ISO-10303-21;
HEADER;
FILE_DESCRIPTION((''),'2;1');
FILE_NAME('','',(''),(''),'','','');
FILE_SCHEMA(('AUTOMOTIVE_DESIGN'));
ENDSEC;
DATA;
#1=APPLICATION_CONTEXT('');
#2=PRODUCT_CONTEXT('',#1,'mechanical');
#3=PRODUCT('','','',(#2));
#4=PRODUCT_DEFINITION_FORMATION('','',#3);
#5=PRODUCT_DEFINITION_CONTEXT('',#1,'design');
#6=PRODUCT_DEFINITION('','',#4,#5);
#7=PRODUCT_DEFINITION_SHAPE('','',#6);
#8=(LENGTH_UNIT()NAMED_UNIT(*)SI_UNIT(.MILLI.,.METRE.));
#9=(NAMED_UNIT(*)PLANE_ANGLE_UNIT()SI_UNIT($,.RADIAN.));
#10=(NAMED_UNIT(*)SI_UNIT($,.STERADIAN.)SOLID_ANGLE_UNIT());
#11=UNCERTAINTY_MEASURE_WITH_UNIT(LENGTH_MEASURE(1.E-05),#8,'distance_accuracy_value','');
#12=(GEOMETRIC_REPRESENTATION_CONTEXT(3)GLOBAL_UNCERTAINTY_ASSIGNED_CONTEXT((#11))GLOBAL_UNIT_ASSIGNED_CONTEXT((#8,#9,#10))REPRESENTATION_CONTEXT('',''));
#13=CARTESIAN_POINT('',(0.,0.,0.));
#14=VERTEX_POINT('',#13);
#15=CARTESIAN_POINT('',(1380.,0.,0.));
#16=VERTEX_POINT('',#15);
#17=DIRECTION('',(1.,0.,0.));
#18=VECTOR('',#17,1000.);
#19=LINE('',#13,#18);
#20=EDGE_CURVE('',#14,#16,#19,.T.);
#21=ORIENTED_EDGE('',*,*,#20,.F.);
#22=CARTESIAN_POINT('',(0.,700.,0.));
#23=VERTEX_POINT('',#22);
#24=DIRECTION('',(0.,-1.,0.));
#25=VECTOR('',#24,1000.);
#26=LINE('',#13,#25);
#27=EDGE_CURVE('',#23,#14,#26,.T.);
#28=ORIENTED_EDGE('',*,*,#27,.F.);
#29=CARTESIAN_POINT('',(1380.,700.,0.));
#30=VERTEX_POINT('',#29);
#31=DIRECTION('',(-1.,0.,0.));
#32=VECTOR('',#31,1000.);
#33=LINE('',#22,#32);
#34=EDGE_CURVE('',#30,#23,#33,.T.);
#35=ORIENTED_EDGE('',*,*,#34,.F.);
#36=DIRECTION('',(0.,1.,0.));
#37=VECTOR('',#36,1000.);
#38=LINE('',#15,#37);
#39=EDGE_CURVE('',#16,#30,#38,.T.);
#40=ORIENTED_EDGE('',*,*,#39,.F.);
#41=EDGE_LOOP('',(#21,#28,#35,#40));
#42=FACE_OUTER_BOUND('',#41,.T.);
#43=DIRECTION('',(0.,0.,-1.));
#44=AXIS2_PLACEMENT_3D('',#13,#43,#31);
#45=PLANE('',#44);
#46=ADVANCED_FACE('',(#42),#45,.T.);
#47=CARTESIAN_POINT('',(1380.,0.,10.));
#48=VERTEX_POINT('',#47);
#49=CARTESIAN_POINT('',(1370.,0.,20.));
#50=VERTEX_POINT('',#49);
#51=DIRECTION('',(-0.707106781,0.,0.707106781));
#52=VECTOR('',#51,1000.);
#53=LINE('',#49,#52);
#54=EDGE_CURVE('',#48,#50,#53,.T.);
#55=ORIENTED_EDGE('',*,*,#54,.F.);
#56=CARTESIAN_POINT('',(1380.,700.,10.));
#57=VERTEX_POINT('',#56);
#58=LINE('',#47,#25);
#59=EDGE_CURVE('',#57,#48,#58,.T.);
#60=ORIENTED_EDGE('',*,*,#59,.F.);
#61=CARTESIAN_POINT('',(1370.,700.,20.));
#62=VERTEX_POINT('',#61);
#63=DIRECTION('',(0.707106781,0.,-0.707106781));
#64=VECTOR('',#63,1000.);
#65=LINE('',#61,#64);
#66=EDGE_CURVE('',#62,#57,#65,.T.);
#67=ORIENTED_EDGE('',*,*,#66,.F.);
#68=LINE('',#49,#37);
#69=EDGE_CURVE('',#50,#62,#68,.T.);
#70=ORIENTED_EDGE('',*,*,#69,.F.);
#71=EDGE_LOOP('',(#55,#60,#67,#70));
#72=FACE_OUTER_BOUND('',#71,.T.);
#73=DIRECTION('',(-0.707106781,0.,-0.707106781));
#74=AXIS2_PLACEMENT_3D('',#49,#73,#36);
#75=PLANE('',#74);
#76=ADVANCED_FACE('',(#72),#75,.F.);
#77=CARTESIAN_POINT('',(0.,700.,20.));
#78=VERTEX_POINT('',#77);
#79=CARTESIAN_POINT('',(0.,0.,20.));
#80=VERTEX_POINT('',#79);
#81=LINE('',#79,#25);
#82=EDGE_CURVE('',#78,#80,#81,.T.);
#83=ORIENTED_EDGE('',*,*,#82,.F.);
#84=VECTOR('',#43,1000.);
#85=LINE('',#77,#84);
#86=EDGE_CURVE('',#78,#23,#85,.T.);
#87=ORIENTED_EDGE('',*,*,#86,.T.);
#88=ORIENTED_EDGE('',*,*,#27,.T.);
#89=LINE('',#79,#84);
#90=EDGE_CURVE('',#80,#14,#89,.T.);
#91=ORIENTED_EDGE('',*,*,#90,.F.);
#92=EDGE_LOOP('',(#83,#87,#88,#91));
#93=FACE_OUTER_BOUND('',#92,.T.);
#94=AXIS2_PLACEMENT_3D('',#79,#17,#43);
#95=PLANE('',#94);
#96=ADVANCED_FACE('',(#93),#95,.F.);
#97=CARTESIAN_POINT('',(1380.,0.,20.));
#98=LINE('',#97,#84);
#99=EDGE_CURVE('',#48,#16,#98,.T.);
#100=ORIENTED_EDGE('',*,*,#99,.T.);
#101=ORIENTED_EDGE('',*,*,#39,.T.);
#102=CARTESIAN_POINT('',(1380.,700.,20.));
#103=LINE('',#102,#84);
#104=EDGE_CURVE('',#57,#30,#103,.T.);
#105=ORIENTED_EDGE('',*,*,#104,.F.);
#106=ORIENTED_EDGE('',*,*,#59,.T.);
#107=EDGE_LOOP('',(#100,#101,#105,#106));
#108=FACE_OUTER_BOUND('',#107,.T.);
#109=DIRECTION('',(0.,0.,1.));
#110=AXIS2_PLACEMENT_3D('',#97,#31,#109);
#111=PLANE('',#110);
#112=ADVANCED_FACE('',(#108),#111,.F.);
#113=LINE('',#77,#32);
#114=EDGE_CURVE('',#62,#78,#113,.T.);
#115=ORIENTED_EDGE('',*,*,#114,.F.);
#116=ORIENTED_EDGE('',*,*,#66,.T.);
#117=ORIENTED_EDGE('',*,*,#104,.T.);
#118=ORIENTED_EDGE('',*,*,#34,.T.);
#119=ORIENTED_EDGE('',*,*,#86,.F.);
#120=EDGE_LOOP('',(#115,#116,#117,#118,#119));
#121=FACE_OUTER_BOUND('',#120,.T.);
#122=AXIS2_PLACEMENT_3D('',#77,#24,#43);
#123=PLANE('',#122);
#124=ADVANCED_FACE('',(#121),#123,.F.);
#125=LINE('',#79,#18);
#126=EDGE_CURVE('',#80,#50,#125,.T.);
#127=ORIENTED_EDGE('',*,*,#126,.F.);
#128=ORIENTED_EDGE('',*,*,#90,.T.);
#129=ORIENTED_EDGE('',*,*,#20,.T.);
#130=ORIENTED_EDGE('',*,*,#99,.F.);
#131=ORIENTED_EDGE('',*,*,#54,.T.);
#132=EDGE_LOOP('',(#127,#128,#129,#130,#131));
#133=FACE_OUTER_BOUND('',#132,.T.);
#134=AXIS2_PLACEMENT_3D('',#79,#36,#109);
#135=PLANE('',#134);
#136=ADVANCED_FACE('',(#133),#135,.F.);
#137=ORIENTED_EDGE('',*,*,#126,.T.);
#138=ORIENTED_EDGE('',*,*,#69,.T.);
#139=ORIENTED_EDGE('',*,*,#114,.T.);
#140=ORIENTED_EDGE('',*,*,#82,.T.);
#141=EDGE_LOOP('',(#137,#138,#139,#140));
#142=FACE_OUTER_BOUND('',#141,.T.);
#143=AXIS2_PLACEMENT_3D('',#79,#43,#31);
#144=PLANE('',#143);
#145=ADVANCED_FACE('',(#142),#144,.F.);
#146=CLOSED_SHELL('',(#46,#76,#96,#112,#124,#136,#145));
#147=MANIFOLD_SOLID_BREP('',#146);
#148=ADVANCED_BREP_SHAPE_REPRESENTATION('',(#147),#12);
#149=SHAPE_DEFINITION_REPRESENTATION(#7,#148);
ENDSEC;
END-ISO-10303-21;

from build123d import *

# Parameters (mm, degrees)
SKETCH1_W           = 1380
SKETCH1_H           = 700
BOSS_EXTRUDE1_DEPTH = 20
CHAMFER1_SIZE       = 10


with BuildPart() as part:
    # Sketch1 → Boss-Extrude1 (new body)
    with BuildSketch(Plane.XY):
        with Locations((690, 350)):
            Rectangle(SKETCH1_W, SKETCH1_H)
    extrude(amount=BOSS_EXTRUDE1_DEPTH)

    # Chamfer1
    chamfer1_edges = [part.edges().sort_by_distance(p)[0] for p in [
        (1380, 350, 20),
    ]]
    chamfer(chamfer1_edges, length=CHAMFER1_SIZE)


solid = part.part
